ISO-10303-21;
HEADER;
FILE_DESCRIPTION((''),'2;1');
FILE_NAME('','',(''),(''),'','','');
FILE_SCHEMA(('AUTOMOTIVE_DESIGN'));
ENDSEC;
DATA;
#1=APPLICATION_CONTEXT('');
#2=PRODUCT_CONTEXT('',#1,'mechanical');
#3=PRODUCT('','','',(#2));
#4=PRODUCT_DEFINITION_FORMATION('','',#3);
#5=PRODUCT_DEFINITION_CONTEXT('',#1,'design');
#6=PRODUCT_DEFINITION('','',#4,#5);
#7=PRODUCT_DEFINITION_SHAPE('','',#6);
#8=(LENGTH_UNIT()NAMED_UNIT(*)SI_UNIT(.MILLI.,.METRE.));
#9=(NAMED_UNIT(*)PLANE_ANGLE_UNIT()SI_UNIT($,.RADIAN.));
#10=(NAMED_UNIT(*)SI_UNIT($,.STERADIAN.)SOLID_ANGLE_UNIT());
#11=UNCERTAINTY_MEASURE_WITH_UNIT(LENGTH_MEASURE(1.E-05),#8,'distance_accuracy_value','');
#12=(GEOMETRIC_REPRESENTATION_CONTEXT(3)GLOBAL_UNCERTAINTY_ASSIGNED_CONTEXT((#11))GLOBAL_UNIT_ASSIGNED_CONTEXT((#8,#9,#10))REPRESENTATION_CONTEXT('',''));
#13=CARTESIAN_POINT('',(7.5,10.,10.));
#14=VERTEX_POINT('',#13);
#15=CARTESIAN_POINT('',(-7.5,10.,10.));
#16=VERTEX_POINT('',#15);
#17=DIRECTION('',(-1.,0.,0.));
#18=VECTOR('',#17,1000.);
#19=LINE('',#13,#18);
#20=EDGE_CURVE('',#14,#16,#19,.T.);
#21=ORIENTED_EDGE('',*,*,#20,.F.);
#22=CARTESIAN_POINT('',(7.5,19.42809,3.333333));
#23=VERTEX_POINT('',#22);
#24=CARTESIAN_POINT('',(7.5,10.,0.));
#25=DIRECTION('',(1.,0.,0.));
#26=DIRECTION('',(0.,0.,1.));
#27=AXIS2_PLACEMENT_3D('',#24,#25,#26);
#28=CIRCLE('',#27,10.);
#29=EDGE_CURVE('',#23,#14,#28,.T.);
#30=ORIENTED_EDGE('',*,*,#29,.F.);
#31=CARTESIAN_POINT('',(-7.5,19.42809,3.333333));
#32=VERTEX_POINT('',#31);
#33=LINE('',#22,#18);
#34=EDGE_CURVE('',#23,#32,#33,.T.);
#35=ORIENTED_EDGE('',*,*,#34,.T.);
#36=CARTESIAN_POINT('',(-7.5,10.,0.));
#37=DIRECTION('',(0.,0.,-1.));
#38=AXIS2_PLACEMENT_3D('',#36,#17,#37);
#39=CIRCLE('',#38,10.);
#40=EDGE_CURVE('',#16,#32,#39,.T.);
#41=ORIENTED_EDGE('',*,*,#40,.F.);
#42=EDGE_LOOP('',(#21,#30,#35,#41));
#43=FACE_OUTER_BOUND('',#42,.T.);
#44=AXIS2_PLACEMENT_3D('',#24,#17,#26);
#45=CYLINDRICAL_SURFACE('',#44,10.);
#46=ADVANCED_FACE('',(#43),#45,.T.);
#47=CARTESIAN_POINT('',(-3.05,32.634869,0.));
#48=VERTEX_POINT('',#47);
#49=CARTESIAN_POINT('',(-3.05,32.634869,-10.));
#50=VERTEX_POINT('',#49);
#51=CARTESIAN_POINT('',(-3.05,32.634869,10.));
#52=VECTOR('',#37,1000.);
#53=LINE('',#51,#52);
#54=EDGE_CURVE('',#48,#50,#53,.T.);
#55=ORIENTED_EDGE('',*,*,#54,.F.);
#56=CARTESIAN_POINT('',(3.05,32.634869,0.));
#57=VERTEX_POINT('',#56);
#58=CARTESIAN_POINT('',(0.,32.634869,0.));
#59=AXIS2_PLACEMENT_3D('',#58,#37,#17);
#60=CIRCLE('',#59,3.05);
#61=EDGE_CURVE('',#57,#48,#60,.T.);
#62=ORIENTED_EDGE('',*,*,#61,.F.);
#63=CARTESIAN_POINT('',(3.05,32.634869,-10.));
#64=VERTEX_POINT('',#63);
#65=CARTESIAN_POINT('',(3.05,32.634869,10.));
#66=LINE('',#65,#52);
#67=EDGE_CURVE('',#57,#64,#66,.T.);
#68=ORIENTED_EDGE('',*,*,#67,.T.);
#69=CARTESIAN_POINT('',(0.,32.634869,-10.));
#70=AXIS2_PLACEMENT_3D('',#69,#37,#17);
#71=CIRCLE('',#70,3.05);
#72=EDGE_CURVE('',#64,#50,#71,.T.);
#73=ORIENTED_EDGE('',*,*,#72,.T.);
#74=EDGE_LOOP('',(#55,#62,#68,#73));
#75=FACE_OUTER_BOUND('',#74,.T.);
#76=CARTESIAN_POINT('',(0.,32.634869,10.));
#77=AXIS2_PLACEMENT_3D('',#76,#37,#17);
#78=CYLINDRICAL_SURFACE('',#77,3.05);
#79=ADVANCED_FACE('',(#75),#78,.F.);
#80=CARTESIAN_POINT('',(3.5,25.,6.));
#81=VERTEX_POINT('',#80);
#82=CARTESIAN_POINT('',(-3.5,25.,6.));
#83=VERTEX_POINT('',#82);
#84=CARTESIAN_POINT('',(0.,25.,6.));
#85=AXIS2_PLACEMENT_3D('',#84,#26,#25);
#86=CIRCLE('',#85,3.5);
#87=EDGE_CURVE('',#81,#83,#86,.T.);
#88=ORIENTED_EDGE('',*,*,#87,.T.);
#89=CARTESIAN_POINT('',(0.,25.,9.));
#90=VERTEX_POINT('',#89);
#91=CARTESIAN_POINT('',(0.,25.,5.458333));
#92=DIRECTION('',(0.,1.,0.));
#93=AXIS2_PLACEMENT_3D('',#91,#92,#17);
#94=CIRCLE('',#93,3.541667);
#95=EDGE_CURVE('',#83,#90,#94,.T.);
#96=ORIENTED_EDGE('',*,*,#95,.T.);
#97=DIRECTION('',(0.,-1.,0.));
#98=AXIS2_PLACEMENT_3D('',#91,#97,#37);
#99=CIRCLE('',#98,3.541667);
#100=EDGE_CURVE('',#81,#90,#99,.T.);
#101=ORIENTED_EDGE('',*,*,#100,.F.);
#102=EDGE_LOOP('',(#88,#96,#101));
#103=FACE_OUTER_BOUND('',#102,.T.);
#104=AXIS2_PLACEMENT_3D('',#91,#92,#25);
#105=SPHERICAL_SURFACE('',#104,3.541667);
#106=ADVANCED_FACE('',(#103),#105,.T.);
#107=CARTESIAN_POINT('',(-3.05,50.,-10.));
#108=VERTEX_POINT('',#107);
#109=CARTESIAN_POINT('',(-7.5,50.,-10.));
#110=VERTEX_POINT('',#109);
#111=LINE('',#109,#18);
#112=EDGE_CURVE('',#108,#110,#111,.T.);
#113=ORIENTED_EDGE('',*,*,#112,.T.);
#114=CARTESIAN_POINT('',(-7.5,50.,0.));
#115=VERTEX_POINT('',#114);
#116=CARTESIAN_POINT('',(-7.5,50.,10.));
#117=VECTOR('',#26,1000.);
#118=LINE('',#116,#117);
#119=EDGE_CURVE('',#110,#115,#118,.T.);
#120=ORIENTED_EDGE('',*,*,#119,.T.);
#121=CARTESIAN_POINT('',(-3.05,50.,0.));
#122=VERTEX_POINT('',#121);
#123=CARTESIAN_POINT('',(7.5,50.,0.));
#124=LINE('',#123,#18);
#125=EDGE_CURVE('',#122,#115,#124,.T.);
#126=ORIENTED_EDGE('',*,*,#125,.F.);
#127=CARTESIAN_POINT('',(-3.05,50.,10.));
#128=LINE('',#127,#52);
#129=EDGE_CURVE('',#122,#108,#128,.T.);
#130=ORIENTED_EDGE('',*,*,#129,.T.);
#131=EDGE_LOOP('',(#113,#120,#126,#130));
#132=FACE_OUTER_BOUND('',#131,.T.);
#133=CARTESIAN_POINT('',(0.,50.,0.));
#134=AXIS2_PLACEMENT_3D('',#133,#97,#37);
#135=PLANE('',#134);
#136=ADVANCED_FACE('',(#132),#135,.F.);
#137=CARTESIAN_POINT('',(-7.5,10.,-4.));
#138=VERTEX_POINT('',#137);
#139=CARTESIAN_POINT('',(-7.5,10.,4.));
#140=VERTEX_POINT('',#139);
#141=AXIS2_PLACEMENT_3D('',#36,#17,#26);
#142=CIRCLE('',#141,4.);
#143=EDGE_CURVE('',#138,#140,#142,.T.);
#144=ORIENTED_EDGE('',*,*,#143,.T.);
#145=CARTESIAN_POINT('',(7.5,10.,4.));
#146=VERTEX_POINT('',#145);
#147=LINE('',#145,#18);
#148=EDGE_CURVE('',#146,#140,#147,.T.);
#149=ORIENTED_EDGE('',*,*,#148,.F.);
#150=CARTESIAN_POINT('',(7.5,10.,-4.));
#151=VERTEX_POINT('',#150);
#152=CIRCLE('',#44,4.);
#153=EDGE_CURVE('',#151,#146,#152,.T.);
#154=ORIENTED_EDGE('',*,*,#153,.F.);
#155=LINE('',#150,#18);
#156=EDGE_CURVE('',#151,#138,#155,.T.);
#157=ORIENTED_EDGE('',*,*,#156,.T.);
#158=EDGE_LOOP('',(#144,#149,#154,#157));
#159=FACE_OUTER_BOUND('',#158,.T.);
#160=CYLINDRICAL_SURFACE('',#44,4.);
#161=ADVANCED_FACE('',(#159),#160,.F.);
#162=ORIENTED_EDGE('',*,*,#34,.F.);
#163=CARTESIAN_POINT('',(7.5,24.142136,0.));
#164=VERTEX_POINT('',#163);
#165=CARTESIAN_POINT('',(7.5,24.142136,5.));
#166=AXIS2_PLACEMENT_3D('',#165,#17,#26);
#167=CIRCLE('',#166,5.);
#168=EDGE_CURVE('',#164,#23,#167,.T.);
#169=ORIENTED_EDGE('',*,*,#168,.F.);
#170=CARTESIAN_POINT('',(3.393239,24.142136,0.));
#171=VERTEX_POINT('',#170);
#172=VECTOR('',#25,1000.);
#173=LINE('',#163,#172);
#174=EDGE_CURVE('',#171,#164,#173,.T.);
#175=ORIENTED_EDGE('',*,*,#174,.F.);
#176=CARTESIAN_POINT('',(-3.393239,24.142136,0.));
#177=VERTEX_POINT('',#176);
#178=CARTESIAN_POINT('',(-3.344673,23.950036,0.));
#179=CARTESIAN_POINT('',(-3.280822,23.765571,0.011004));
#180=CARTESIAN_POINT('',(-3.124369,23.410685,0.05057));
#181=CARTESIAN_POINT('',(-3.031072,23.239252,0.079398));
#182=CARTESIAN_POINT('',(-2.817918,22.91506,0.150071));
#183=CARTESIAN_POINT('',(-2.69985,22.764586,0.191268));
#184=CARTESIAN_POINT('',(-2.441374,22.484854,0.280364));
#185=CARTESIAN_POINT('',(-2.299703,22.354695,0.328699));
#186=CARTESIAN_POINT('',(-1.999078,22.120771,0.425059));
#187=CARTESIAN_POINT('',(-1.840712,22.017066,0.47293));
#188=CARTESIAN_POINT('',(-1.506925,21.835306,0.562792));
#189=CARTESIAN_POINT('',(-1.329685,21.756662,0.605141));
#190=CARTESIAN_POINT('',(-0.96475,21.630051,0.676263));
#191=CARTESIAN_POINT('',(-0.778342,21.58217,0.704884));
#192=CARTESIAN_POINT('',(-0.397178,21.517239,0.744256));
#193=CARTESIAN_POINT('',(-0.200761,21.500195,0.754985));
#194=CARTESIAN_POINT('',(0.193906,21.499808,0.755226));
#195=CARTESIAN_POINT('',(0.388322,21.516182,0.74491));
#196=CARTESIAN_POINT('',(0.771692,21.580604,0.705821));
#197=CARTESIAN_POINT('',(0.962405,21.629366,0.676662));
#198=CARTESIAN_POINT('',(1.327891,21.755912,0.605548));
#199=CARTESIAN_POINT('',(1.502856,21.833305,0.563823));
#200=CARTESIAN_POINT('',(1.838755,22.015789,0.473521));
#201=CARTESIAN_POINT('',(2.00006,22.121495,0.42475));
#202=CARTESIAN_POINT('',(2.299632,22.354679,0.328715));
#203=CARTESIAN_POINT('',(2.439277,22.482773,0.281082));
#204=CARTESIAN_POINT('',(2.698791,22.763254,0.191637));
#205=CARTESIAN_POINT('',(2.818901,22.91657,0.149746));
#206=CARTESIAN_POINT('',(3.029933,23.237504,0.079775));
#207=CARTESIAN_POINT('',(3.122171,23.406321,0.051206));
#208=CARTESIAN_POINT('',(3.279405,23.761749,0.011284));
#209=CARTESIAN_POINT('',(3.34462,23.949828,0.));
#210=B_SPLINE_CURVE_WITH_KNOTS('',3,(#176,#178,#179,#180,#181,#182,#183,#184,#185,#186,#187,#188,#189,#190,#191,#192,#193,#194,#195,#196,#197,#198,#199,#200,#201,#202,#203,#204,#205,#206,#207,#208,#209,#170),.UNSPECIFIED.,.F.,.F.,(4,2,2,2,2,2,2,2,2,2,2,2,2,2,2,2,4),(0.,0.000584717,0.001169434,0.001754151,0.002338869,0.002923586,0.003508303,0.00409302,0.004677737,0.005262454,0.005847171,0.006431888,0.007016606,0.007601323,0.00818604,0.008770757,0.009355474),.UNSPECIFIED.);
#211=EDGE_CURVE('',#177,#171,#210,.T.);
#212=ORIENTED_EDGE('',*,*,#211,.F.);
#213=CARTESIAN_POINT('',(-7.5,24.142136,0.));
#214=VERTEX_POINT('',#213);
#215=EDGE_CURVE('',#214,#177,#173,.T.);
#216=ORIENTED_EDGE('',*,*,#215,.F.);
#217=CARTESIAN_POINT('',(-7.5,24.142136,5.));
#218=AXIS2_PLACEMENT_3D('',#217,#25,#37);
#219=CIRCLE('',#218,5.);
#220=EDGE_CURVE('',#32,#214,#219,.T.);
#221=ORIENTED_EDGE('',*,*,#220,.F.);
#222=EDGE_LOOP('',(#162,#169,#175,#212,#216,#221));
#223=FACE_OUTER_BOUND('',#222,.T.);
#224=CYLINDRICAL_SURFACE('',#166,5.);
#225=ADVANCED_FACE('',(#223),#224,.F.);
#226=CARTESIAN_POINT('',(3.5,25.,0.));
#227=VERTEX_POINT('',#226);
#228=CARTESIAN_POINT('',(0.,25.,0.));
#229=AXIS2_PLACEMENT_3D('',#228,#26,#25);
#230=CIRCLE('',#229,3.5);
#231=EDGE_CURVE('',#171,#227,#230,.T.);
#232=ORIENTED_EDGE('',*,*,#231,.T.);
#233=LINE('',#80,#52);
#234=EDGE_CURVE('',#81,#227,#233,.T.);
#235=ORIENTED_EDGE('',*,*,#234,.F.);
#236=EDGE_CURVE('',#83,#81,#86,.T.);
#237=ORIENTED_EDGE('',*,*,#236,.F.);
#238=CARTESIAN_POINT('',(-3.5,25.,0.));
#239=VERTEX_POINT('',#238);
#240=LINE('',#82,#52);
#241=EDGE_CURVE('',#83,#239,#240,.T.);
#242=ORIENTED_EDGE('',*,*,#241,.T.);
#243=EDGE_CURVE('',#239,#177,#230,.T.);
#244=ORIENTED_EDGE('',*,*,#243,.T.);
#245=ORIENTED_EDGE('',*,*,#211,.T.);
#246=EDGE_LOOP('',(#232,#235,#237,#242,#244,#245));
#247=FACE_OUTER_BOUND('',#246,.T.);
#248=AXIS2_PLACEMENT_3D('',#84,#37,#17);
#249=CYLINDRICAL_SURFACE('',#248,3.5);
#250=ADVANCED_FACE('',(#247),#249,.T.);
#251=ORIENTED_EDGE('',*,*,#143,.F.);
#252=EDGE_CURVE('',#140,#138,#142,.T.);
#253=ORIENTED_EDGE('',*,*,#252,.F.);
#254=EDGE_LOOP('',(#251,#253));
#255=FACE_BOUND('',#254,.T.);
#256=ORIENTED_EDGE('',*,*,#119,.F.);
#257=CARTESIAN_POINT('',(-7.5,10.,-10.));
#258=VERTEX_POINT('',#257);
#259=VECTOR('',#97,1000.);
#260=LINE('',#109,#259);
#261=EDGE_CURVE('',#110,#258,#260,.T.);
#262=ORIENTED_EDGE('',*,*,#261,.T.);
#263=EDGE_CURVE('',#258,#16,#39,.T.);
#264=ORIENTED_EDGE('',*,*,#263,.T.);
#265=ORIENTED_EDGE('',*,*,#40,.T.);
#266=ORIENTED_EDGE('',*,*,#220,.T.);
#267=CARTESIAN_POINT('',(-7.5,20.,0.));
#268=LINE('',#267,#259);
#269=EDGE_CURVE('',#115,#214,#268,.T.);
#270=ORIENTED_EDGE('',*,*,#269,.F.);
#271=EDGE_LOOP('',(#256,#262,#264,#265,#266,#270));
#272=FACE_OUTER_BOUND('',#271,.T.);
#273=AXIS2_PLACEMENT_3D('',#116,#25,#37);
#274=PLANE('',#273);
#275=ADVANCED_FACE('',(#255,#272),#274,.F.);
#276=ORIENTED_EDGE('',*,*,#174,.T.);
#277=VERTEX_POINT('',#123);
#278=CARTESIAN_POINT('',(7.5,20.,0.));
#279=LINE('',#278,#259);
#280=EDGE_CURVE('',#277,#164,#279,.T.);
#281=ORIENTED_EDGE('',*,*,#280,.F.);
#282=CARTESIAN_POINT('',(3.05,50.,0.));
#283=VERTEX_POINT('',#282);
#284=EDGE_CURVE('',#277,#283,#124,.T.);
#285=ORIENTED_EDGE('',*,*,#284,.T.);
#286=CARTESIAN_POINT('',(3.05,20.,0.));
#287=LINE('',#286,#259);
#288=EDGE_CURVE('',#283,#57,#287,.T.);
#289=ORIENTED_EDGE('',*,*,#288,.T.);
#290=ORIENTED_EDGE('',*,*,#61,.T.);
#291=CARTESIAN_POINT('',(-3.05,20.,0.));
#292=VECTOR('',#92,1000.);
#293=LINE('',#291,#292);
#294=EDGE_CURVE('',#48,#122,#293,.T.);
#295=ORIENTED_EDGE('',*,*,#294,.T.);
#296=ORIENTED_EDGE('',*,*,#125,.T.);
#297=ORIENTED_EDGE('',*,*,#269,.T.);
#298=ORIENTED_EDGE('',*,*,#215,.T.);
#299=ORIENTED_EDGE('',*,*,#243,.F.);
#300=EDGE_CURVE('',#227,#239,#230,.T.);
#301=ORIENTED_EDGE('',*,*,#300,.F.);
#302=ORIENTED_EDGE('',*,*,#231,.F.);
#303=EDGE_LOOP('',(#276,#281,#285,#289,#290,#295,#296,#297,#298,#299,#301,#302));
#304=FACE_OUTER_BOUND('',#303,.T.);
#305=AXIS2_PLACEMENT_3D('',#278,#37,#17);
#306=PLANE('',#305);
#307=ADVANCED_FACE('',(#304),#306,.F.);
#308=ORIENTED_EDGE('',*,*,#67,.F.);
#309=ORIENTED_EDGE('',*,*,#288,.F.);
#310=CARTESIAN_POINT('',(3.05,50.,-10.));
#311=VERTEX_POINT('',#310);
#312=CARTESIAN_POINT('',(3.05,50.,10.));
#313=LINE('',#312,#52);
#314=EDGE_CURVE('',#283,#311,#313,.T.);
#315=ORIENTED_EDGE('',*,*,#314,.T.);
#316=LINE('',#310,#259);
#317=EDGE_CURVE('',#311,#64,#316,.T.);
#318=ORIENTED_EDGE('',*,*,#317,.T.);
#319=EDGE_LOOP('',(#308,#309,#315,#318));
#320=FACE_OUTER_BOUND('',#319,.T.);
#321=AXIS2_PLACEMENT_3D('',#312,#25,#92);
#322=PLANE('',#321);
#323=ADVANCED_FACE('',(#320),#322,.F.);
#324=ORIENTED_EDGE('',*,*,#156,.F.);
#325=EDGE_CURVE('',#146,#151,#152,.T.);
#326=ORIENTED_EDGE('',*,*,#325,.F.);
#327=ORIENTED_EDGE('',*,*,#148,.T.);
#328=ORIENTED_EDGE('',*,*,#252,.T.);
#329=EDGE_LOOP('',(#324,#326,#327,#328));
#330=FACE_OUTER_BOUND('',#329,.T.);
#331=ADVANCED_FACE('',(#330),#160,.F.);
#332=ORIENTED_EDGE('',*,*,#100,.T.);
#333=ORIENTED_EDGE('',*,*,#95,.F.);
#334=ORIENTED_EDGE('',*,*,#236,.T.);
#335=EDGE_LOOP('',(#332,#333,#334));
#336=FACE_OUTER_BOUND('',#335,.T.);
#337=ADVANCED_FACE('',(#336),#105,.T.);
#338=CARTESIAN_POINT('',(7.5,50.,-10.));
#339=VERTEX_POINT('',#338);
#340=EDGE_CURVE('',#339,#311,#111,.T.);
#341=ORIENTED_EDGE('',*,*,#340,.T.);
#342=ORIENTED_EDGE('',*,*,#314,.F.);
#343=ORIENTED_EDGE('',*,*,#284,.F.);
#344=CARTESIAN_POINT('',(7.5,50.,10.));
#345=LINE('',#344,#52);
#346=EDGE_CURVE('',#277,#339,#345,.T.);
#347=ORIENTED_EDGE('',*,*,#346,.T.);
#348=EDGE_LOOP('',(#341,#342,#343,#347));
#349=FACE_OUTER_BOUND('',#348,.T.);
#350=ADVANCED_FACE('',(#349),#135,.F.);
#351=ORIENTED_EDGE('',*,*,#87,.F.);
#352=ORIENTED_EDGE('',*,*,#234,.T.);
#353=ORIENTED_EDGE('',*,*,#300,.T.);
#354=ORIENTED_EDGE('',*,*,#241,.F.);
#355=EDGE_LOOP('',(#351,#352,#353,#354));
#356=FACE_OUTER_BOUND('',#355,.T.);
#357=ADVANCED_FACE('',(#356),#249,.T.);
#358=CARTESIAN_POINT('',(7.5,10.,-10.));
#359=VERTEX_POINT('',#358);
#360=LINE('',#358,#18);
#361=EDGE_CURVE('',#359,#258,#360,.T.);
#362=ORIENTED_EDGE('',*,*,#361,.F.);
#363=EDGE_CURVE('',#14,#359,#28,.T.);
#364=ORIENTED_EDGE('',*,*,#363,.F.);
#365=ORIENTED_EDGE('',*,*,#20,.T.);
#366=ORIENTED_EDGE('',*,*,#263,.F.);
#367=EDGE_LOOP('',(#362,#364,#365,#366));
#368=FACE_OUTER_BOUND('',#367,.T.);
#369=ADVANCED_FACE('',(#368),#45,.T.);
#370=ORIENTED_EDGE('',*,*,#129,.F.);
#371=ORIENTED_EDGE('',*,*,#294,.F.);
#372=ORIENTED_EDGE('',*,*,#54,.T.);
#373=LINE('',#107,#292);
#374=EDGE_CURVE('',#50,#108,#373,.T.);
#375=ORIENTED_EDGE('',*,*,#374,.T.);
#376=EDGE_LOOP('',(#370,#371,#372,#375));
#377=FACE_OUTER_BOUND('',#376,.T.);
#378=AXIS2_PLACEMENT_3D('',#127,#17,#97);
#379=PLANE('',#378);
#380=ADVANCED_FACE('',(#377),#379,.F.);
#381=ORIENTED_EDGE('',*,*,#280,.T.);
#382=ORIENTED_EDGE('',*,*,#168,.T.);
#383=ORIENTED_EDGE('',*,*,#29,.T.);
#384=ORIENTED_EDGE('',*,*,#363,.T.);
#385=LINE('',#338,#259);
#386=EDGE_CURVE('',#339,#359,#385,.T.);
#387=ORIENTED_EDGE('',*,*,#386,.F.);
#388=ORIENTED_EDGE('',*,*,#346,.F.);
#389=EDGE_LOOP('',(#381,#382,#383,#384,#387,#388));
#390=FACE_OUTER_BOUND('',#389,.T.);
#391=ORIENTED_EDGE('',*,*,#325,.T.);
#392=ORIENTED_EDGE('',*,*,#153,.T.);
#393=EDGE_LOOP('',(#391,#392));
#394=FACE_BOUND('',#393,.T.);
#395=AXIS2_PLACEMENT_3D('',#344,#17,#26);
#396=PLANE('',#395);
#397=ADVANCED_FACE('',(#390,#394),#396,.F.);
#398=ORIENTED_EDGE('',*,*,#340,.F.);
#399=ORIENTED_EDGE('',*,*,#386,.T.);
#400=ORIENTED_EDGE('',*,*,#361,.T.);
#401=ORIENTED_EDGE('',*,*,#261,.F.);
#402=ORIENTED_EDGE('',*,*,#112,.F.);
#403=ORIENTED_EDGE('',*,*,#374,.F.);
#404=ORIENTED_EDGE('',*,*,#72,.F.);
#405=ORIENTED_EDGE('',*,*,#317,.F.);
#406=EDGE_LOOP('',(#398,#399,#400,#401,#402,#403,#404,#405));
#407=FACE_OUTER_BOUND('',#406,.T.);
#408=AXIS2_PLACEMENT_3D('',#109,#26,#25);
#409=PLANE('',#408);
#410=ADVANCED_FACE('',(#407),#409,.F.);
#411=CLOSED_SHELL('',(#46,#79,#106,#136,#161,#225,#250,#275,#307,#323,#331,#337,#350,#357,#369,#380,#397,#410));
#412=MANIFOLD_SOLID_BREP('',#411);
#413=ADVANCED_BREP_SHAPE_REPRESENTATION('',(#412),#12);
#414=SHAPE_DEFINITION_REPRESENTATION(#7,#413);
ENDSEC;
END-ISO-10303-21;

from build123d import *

# Parameters (mm, degrees)
SKETCH1_W           = 15
SKETCH1_H           = 20
BOSS_EXTRUDE1_DEPTH = 50
FILLET1_RADIUS      = 10
FILLET1_LENGTH      = 15
SKETCH2_R           = 4
CUT_EXTRUDE1_DEPTH  = 54.150729064
CUT_EXTRUDE2_DEPTH  = 54.150729064
FILLET2_R           = 5
SKETCH4_R           = 3.5
BOSS_EXTRUDE2_DEPTH = 6
DOME1_FACE_RADIUS   = 3.5
DOME1_HEIGHT        = 3
CUT_EXTRUDE3_DEPTH  = 55.371407941


with BuildPart() as part:
    # Sketch1 → Boss-Extrude1 (new body)
    with BuildSketch(Plane(origin=(0, 0, 0), x_dir=(1, 0, 0), z_dir=(0, 1, 0))):
        Rectangle(SKETCH1_W, SKETCH1_H)
    extrude(amount=BOSS_EXTRUDE1_DEPTH)

    # Fillet1: full round fillet: the end face becomes a half cylinder, R = half its width
    fillet1_face = Plane((0, 0, 0), x_dir=(-1, 0, 0), z_dir=(0, -1, 0))  # on the end face: x along it, z out of the body
    fillet1_slab = fillet1_face.offset(-FILLET1_RADIUS / 2) * Box(FILLET1_LENGTH, 2 * FILLET1_RADIUS, FILLET1_RADIUS, mode=Mode.PRIVATE)  # the body's end, R deep
    fillet1_round = Plane((0, 10, 0), x_dir=(0, -1, 0), z_dir=(-1, 0, 0)) * Cylinder(FILLET1_RADIUS, FILLET1_LENGTH, mode=Mode.PRIVATE)  # its axis R under the face
    add(fillet1_slab - fillet1_round, mode=Mode.SUBTRACT)

    # Sketch2 → Cut-Extrude1 (cut, through all)
    with BuildSketch(Plane.ZY.offset(7.5)):
        with Locations((0, 10)):
            Circle(SKETCH2_R)
    extrude(amount=-CUT_EXTRUDE1_DEPTH, mode=Mode.SUBTRACT)

    # Sketch3 → Cut-Extrude2 (cut, through all)
    with BuildSketch(Plane.ZY.offset(7.5)):
        with BuildLine():
            Line((0, 20), (0, 50))
            Line((0, 50), (10, 50))
            Line((10, 50), (10, 10))
            ThreePointArc((10, 10), (7.071067812, 17.071067812), (0, 20))
        make_face()
    extrude(amount=-CUT_EXTRUDE2_DEPTH, mode=Mode.SUBTRACT)

    # Fillet2
    fillet2_edges = [part.edges().sort_by_distance(p)[0] for p in [
        (0, 20, 0),
    ]]
    fillet(fillet2_edges, radius=FILLET2_R)

    # Sketch4 → Boss-Extrude2 (add)
    with BuildSketch(Plane.XY):
        with Locations(Location((0, 25, 0), (0, 0, 194.18798624))):
            Circle(SKETCH4_R)
    extrude(amount=BOSS_EXTRUDE2_DEPTH)

    # Dome1: a dome of height H over a round flat face of radius A is a cap of a sphere of radius (A * A + H * H) / (2 * H)
    dome1_r = (DOME1_FACE_RADIUS * DOME1_FACE_RADIUS + DOME1_HEIGHT * DOME1_HEIGHT) / (2 * DOME1_HEIGHT)
    dome1_base = Plane((0, 25, 6), z_dir=(0, 0, 1))
    with Locations(dome1_base.offset(DOME1_HEIGHT - dome1_r)):
        dome1_ball = Sphere(dome1_r, mode=Mode.PRIVATE)
    add(split(dome1_ball, bisect_by=dome1_base, keep=Keep.TOP, mode=Mode.PRIVATE))

    # Sketch5 → Cut-Extrude3 (cut, through all)
    with BuildSketch(Plane(origin=(0, 0, -10), x_dir=(-1, 0, 0), z_dir=(0, 0, -1))):
        with BuildLine():
            Line((3.05, 50), (3.05, 32.634868852))
            ThreePointArc((3.05, 32.634868852), (0, 29.584868852), (-3.05, 32.634868852))
            Line((-3.05, 32.634868852), (-3.05, 50))
            ThreePointArc((-3.05, 50), (0, 53.05), (3.05, 50))
        make_face()
    extrude(amount=-CUT_EXTRUDE3_DEPTH, mode=Mode.SUBTRACT)


solid = part.part
